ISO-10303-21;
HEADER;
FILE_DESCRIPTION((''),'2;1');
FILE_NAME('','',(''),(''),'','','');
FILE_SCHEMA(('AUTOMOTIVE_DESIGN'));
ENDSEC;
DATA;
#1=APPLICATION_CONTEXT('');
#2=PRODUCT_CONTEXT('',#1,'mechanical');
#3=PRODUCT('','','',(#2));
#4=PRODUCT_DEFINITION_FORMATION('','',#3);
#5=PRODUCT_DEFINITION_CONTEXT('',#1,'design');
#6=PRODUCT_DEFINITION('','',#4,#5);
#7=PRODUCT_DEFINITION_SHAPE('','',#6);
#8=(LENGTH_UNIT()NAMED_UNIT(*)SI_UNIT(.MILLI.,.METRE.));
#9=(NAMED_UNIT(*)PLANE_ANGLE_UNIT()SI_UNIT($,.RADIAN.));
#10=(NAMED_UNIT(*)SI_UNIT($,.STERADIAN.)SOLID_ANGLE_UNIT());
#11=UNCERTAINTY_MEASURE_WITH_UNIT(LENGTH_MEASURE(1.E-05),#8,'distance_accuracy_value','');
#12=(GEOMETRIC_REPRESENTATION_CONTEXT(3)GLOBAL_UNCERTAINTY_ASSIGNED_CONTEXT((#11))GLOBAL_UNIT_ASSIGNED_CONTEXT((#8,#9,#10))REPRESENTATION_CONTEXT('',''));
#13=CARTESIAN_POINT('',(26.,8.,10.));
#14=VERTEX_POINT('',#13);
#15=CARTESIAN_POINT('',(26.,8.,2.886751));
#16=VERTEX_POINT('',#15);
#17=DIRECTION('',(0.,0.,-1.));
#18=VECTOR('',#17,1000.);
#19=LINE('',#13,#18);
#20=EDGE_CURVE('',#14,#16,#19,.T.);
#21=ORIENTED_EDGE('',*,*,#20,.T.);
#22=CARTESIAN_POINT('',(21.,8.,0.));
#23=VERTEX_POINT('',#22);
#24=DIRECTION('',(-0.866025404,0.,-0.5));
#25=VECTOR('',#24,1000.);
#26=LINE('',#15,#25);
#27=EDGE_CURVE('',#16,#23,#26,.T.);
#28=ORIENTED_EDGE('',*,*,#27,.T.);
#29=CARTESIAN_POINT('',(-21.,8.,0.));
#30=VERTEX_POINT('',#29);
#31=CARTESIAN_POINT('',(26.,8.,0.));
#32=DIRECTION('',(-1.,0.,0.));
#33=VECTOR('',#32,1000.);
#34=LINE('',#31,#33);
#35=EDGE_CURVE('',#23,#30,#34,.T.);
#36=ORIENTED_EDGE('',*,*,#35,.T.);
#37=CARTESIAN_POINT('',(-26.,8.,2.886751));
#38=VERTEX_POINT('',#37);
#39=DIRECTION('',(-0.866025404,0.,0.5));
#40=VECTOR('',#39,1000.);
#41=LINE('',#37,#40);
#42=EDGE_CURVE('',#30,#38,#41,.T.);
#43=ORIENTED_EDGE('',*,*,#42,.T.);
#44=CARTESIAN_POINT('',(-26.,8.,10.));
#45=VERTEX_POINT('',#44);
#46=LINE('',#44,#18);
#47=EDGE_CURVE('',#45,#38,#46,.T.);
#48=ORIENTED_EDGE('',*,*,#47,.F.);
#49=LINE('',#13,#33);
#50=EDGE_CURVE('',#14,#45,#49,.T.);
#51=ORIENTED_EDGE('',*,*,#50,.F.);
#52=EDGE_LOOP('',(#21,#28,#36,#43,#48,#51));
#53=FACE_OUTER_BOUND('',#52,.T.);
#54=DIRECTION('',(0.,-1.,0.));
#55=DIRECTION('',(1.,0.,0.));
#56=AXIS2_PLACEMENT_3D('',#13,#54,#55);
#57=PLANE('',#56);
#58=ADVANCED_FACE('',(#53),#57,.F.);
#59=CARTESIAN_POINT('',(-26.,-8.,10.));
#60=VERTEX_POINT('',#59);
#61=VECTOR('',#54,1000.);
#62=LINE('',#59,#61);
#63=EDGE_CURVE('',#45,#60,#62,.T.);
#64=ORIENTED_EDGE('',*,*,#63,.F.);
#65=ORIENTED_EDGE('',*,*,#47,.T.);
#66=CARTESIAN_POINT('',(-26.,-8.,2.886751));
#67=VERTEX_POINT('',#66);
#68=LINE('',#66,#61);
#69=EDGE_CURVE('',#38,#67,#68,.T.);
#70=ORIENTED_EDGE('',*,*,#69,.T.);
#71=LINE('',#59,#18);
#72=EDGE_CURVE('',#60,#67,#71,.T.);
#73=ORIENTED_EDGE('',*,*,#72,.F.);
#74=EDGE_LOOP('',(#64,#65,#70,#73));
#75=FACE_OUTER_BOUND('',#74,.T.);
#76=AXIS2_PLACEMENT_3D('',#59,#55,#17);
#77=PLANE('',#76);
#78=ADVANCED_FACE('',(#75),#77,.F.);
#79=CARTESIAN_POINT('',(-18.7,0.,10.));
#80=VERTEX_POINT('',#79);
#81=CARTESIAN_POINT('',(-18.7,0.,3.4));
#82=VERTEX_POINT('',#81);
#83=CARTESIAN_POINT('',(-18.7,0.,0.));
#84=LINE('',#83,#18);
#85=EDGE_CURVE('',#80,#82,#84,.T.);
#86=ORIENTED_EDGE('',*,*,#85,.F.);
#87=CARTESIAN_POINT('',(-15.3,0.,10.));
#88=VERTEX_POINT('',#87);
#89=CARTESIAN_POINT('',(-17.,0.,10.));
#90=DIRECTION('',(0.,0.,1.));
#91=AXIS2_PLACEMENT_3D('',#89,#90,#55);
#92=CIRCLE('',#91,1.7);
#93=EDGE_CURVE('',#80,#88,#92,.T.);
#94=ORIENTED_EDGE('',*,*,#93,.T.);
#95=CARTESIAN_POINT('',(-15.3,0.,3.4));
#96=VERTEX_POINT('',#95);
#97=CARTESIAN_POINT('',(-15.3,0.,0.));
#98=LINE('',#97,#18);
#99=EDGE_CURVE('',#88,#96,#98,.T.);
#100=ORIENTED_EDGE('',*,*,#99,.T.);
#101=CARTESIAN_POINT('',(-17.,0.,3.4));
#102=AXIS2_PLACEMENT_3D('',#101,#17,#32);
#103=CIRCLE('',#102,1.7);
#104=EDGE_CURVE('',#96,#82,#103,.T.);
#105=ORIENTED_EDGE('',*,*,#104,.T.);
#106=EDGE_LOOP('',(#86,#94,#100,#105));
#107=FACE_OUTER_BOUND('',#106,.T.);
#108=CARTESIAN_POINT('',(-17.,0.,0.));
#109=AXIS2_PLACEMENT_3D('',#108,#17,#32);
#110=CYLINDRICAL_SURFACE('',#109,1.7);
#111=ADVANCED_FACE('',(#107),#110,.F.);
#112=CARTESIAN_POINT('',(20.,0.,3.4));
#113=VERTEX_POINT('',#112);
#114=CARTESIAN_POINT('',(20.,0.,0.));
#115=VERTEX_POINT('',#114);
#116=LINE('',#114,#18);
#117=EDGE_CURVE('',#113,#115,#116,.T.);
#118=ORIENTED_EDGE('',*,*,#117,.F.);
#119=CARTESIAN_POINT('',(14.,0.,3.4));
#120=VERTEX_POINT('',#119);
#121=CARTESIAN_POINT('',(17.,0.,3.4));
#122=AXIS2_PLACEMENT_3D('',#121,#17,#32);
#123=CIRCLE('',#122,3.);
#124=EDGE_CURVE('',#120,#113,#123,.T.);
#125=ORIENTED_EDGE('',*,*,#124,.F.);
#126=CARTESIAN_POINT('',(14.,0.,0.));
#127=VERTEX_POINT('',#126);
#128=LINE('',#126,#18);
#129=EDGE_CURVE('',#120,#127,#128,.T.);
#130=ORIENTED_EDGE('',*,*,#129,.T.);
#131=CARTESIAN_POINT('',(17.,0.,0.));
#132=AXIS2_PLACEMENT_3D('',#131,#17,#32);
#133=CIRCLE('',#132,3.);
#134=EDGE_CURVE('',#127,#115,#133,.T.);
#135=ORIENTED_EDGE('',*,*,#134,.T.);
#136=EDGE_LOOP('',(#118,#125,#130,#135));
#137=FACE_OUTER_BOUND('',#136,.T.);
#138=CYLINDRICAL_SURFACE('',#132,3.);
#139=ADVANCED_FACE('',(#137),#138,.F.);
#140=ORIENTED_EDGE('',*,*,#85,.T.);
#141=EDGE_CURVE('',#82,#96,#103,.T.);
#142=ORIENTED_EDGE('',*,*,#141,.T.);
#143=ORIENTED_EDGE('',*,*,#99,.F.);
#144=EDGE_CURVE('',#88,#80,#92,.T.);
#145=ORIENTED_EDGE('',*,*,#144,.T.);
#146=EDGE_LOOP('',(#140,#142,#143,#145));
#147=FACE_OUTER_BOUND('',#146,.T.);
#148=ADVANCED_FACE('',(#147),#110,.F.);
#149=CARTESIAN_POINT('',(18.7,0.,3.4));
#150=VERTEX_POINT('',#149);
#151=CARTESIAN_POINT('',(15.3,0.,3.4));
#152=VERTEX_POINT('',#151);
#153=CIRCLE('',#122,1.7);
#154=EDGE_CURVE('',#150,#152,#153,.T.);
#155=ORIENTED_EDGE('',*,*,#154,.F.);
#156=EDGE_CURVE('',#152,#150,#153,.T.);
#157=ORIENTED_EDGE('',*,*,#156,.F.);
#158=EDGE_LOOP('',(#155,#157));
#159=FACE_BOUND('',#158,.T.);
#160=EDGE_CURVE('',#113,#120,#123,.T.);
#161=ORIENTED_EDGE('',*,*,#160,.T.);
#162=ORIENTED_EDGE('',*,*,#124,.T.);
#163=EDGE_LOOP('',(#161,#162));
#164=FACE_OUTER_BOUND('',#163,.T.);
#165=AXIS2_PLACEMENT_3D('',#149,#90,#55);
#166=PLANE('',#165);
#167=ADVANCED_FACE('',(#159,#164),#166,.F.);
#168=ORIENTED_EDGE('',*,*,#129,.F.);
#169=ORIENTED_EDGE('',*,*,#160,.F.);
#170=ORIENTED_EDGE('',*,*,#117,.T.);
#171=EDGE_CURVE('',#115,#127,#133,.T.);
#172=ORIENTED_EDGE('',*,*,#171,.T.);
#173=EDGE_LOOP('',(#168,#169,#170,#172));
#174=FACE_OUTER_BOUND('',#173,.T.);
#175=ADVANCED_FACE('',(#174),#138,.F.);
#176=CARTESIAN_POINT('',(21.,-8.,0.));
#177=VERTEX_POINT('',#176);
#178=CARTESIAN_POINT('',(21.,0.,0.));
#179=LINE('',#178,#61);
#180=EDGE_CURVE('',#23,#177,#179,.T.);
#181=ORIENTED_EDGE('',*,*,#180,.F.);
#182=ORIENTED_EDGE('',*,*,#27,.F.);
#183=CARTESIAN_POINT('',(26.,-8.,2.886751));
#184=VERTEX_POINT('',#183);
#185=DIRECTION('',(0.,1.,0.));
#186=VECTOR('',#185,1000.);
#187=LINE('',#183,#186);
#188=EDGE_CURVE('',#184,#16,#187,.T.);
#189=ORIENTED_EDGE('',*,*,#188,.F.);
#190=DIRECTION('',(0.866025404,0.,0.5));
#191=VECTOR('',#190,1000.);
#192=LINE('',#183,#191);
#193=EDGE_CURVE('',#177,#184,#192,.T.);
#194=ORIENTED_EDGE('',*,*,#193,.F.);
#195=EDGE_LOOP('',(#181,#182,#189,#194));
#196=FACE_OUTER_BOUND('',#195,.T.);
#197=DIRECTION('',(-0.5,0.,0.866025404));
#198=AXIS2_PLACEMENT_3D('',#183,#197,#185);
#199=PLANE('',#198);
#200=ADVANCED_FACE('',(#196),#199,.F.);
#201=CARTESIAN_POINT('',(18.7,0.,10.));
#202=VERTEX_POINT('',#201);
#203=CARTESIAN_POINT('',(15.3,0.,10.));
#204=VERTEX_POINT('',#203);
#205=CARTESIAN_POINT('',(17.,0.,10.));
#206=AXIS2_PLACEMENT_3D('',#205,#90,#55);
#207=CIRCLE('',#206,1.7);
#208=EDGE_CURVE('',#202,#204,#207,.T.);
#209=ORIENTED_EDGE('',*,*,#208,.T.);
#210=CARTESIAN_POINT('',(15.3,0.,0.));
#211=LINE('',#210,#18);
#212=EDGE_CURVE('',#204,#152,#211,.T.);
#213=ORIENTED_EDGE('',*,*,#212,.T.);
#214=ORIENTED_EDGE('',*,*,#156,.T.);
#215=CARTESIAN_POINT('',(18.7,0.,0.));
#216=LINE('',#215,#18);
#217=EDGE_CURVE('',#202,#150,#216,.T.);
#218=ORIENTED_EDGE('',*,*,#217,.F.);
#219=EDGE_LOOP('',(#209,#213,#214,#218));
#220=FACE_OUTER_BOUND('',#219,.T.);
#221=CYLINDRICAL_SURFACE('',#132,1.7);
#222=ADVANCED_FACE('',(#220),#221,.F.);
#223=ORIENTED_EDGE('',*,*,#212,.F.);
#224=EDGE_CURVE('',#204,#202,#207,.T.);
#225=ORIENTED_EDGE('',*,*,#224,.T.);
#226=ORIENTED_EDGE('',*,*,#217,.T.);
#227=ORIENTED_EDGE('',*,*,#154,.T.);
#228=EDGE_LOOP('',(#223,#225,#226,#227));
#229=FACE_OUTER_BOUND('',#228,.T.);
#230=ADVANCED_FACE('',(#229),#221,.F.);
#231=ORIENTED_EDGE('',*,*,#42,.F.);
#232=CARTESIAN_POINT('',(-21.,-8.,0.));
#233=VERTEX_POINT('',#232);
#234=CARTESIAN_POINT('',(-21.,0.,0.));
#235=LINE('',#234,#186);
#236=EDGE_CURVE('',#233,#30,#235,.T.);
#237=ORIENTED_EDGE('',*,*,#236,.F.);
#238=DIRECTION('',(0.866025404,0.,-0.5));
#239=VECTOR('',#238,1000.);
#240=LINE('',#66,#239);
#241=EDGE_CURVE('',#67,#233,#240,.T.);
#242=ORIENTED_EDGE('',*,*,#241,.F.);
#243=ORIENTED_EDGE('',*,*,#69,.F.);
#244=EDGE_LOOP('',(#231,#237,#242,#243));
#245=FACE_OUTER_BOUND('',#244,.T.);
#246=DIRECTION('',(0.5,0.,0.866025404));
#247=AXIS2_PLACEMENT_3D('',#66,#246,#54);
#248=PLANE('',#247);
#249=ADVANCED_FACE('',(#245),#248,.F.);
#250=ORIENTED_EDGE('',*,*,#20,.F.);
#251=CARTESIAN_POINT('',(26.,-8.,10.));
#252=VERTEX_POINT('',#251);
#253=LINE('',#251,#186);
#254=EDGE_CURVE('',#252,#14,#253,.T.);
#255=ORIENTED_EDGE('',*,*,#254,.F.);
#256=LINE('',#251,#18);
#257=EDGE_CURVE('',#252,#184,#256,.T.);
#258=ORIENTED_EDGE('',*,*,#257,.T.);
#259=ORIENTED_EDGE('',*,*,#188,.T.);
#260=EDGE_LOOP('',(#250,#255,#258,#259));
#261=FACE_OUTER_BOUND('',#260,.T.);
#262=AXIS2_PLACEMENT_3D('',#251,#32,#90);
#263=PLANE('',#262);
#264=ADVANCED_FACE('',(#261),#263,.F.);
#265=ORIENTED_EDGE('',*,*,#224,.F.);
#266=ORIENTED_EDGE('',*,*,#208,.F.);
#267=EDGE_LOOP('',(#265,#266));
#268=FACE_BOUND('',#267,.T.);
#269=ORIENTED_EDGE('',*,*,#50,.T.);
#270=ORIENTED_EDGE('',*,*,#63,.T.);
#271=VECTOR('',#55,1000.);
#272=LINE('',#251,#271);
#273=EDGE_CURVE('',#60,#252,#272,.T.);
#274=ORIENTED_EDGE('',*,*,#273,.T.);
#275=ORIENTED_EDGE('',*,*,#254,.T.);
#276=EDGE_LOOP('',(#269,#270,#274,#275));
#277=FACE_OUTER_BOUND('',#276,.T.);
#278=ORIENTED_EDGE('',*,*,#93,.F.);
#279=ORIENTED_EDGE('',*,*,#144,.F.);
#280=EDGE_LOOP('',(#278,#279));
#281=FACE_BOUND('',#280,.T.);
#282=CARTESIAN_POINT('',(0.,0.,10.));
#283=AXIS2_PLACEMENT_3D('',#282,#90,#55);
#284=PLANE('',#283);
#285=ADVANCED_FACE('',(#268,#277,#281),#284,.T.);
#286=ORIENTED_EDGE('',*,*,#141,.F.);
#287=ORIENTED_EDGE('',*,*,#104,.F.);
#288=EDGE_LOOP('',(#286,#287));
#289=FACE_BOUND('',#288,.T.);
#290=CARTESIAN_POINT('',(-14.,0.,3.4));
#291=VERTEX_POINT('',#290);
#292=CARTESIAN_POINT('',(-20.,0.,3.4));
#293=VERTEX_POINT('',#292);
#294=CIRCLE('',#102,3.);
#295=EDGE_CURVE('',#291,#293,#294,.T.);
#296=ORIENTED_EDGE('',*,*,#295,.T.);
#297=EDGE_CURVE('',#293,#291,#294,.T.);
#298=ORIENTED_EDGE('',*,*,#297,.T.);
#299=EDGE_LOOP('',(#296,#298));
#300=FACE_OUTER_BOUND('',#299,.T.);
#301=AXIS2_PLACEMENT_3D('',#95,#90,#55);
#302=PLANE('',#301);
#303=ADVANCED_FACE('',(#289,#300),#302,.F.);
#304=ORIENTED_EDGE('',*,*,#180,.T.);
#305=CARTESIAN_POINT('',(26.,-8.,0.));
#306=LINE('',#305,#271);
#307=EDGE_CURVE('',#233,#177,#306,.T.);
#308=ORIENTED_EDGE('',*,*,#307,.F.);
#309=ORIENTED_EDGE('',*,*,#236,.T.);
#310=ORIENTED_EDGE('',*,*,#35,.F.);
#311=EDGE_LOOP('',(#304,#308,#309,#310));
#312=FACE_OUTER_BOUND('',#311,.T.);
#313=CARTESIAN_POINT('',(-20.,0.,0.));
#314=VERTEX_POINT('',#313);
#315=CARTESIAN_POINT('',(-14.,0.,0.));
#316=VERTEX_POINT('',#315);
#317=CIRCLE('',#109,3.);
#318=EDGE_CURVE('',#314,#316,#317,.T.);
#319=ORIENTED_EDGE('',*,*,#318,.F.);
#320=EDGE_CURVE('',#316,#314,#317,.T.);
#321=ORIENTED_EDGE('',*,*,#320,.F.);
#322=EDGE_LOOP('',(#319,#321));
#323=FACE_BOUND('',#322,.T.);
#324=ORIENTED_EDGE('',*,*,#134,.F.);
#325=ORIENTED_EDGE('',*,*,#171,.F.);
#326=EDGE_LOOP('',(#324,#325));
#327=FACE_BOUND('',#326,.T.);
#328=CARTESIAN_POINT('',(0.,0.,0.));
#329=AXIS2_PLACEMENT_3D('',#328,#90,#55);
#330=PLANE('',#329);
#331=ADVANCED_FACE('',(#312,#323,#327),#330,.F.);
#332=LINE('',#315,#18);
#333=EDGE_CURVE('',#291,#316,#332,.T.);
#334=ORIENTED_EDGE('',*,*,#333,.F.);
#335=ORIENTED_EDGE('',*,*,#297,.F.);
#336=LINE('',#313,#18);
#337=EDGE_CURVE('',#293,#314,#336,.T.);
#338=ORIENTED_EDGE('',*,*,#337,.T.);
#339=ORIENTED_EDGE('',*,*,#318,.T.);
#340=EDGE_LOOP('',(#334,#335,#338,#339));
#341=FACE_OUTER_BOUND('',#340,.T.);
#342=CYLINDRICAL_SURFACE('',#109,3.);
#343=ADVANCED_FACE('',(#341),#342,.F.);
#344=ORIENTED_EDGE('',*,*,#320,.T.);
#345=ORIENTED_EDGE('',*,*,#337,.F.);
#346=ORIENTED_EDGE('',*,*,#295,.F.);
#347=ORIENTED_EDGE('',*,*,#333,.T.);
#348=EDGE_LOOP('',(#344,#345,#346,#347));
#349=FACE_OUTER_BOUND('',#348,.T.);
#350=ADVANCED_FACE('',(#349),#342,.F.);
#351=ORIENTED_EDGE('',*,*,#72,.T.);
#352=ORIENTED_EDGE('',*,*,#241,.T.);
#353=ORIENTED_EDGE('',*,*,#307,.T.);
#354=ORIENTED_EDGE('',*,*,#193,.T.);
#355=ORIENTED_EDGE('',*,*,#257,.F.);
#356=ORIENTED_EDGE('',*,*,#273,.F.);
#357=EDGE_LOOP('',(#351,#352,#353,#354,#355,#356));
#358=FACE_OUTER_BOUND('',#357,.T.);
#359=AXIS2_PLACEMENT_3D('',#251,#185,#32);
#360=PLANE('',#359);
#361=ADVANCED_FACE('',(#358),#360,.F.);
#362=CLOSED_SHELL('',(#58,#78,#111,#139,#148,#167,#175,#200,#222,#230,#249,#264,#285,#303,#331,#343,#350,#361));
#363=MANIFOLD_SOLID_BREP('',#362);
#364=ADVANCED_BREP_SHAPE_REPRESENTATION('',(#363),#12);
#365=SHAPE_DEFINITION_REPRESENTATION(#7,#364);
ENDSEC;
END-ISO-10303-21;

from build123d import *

# Parameters (mm, degrees)
SKETCH_1_W                = 52
SKETCH_1_H                = 16
EXTRUDE_1_DEPTH           = 10
HOLE_WIZARD_1_D           = 3.4
HOLE_WIZARD_1_DEPTH       = 38
HOLE_WIZARD_1_CBORE_D     = 6
HOLE_WIZARD_1_CBORE_DEPTH = 3.4
HOLE_WIZARD_1_TIP         = 1.021463052
CHAMFER_1_SIZE            = 5
CHAMFER_1_SIZE2           = 2.886751346
CHAMFER_2_SIZE            = 5
CHAMFER_2_SIZE2           = 2.886751346


with BuildPart() as part:
    # 草图1 → 凸台-拉伸1 (new body)
    with BuildSketch(Plane.XY):
        Rectangle(SKETCH_1_W, SKETCH_1_H)
    extrude(amount=EXTRUDE_1_DEPTH)

    # 打孔尺寸(%根据)内六角圆柱头螺钉的类型1
    with Locations(Plane(origin=(0, 0, 0), x_dir=(-1, 0, 0), z_dir=(0, 0, -1))):
        with Locations((-17, 0), (17, 0)):
            CounterBoreHole(HOLE_WIZARD_1_D / 2, HOLE_WIZARD_1_CBORE_D / 2, HOLE_WIZARD_1_CBORE_DEPTH, depth=HOLE_WIZARD_1_DEPTH)
            with Locations((0, 0, -(HOLE_WIZARD_1_DEPTH + HOLE_WIZARD_1_TIP / 2))):  # 118° drill point
                Cone(0, HOLE_WIZARD_1_D / 2, HOLE_WIZARD_1_TIP, mode=Mode.SUBTRACT)

    # 倒角1
    chamfer_1_edges = [part.edges().sort_by_distance(p)[0] for p in [
        (26, 0, 0),
    ]]
    chamfer_1_side = [part.faces().sort_by_distance(p)[0] for p in [
        (0, 0, 0),
    ]]
    chamfer(chamfer_1_edges, length=CHAMFER_1_SIZE, length2=CHAMFER_1_SIZE2, reference=chamfer_1_side[0])

    # 倒角2
    chamfer_2_edges = [part.edges().sort_by_distance(p)[0] for p in [
        (-26, 0, 0),
    ]]
    chamfer_2_side = [part.faces().sort_by_distance(p)[0] for p in [
        (-2.703280464, 0, 0),
    ]]
    chamfer(chamfer_2_edges, length=CHAMFER_2_SIZE, length2=CHAMFER_2_SIZE2, reference=chamfer_2_side[0])


solid = part.part
